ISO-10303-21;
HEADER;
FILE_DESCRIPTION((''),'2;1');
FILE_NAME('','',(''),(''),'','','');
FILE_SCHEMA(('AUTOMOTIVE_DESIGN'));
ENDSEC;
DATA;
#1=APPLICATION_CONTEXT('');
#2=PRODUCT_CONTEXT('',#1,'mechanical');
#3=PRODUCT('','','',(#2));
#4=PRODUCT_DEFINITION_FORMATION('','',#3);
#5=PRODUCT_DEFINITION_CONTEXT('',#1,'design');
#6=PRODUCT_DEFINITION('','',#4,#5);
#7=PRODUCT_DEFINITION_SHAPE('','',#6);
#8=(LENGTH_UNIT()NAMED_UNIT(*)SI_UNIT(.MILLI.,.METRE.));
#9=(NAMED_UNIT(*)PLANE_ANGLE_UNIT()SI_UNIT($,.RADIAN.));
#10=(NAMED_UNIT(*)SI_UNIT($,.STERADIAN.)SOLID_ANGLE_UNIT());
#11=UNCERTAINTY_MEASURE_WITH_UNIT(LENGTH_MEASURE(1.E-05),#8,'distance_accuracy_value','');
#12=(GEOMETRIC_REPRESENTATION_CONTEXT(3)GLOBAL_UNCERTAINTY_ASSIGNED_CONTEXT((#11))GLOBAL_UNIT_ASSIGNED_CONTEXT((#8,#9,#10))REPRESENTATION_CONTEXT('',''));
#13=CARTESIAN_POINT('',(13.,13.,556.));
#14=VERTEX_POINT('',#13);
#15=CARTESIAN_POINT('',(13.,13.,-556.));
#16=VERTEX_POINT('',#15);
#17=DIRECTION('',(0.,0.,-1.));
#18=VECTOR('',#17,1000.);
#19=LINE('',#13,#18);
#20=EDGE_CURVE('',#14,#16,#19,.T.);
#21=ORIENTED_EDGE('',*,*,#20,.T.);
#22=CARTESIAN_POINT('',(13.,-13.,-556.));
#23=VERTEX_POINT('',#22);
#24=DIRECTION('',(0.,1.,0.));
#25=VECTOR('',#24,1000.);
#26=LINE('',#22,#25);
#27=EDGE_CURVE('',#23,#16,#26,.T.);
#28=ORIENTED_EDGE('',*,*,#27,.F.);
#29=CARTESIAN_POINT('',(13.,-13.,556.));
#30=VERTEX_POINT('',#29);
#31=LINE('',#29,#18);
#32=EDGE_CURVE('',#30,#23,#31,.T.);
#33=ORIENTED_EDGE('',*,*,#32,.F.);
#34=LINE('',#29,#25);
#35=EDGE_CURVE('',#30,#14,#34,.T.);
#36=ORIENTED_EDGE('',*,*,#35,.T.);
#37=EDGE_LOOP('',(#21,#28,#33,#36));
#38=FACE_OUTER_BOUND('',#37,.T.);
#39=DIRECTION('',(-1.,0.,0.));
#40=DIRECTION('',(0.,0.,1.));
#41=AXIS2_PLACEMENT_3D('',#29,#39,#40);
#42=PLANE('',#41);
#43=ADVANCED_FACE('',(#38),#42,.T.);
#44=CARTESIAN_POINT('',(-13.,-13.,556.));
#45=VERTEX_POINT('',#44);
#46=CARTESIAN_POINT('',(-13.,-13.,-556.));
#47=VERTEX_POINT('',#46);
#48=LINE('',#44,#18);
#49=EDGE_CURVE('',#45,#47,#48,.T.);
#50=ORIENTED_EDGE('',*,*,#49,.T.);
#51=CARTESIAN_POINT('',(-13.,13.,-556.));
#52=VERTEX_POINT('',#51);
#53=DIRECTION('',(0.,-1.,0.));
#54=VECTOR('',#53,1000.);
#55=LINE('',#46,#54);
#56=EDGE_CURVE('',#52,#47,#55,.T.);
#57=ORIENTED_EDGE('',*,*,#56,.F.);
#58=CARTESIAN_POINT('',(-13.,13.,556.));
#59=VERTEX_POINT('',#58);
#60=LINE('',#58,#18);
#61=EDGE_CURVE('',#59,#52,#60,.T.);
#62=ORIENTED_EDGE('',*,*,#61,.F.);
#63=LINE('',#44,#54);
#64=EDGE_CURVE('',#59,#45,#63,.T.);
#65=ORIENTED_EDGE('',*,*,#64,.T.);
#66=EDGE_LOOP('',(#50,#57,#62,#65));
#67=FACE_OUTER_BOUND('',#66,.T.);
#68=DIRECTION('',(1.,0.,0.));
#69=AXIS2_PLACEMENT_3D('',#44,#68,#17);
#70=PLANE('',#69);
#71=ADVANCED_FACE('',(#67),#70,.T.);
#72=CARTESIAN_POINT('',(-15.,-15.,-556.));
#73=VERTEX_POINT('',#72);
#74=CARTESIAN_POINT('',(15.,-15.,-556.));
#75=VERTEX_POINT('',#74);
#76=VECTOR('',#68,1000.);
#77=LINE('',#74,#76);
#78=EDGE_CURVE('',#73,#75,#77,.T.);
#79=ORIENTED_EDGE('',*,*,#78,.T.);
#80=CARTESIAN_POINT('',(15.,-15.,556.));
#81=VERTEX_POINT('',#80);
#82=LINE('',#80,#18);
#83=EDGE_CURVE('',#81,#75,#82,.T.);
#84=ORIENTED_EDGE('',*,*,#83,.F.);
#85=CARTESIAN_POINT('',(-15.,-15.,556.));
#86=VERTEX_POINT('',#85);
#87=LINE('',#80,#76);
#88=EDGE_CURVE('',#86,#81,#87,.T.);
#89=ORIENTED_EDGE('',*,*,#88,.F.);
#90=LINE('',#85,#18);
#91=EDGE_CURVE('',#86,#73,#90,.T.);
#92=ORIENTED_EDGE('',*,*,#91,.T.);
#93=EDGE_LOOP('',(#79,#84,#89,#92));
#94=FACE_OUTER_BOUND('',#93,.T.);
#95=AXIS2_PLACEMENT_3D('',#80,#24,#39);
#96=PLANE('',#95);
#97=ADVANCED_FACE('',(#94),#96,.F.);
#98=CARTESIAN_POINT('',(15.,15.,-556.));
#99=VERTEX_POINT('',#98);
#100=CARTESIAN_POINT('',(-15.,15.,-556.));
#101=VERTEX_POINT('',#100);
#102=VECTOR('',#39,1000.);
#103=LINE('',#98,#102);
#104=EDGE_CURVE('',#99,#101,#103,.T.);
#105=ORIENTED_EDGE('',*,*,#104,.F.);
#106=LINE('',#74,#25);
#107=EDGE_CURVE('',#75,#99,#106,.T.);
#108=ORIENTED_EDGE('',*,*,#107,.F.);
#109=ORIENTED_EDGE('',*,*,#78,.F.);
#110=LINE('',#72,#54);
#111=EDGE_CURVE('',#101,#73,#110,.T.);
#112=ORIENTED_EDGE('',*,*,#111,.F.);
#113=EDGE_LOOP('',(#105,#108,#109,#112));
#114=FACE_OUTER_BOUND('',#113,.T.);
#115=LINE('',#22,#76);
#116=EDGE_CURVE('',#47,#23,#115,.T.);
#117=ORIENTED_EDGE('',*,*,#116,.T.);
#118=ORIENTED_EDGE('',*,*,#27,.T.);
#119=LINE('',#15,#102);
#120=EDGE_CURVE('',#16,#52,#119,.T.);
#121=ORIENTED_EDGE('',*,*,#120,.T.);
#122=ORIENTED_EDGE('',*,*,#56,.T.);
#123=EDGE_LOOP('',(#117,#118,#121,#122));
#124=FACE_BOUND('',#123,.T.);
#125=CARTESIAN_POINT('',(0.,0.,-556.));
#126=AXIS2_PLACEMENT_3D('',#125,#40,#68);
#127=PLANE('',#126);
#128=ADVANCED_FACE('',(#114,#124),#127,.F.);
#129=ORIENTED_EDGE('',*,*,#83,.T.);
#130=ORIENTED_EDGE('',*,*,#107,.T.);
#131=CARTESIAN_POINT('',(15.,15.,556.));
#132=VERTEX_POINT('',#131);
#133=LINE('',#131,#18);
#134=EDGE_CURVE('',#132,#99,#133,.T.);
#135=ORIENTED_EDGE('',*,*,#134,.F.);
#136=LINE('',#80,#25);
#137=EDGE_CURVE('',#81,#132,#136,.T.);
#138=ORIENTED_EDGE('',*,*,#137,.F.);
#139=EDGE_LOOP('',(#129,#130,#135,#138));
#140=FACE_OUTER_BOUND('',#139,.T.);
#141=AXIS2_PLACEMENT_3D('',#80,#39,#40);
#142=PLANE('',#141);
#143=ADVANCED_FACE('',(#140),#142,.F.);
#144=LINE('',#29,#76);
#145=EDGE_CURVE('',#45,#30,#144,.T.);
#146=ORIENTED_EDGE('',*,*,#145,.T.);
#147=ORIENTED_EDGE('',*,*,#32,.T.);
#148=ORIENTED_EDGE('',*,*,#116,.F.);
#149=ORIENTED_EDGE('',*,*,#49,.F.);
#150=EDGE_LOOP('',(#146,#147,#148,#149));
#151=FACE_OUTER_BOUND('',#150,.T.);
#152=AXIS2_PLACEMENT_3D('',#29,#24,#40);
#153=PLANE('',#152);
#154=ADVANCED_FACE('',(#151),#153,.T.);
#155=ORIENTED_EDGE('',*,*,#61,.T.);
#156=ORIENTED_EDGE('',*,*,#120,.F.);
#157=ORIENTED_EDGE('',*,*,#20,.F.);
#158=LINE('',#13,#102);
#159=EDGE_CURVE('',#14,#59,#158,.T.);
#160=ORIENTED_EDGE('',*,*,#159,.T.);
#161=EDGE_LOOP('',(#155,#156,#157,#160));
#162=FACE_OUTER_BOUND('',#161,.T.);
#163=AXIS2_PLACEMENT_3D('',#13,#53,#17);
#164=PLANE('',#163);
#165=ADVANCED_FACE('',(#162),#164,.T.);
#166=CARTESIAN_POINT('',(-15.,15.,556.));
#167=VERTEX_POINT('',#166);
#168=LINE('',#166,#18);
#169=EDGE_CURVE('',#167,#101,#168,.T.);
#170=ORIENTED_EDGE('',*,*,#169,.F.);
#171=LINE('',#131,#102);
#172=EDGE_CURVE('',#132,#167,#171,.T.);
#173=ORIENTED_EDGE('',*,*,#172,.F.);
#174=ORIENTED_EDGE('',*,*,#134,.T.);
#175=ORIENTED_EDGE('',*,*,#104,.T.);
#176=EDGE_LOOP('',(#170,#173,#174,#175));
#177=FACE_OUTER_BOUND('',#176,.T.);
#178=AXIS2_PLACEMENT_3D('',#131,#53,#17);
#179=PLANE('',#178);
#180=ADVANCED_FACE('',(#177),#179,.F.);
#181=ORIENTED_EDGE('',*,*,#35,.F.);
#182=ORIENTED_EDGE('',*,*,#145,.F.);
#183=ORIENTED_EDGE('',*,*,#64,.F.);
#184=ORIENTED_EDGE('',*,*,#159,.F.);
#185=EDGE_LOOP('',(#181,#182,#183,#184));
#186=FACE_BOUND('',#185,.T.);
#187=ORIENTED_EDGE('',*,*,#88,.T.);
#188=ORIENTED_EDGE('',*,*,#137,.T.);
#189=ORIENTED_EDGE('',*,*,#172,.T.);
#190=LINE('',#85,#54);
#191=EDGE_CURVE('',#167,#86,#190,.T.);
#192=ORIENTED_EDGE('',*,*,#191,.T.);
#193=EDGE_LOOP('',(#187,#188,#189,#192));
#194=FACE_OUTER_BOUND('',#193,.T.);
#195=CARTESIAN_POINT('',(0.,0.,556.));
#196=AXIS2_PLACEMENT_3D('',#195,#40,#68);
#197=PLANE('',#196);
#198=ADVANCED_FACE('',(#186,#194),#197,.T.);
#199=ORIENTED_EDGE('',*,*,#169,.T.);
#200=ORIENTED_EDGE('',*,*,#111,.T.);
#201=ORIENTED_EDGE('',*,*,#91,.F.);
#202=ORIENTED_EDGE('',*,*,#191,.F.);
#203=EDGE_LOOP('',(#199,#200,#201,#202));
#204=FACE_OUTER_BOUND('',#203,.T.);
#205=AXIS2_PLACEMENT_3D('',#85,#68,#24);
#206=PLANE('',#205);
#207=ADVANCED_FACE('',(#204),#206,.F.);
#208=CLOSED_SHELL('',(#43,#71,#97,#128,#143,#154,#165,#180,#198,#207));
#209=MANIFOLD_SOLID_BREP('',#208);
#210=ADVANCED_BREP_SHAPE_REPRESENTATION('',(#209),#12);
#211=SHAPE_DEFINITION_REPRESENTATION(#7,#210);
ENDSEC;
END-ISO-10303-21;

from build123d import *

# Parameters (mm, degrees)
SKETCH_1_W      = 30
SKETCH_1_H      = 30
SKETCH_1_W_2    = 26
SKETCH_1_H_2    = 26
EXTRUDE_1_DEPTH = 556


with BuildPart() as part:
    # 草图1 → 凸台-拉伸1 (new, symmetric)
    with BuildSketch(Plane.XY):
        Rectangle(SKETCH_1_W, SKETCH_1_H)
        Rectangle(SKETCH_1_W_2, SKETCH_1_H_2, mode=Mode.SUBTRACT)
    extrude(amount=EXTRUDE_1_DEPTH, both=True)


solid = part.part
